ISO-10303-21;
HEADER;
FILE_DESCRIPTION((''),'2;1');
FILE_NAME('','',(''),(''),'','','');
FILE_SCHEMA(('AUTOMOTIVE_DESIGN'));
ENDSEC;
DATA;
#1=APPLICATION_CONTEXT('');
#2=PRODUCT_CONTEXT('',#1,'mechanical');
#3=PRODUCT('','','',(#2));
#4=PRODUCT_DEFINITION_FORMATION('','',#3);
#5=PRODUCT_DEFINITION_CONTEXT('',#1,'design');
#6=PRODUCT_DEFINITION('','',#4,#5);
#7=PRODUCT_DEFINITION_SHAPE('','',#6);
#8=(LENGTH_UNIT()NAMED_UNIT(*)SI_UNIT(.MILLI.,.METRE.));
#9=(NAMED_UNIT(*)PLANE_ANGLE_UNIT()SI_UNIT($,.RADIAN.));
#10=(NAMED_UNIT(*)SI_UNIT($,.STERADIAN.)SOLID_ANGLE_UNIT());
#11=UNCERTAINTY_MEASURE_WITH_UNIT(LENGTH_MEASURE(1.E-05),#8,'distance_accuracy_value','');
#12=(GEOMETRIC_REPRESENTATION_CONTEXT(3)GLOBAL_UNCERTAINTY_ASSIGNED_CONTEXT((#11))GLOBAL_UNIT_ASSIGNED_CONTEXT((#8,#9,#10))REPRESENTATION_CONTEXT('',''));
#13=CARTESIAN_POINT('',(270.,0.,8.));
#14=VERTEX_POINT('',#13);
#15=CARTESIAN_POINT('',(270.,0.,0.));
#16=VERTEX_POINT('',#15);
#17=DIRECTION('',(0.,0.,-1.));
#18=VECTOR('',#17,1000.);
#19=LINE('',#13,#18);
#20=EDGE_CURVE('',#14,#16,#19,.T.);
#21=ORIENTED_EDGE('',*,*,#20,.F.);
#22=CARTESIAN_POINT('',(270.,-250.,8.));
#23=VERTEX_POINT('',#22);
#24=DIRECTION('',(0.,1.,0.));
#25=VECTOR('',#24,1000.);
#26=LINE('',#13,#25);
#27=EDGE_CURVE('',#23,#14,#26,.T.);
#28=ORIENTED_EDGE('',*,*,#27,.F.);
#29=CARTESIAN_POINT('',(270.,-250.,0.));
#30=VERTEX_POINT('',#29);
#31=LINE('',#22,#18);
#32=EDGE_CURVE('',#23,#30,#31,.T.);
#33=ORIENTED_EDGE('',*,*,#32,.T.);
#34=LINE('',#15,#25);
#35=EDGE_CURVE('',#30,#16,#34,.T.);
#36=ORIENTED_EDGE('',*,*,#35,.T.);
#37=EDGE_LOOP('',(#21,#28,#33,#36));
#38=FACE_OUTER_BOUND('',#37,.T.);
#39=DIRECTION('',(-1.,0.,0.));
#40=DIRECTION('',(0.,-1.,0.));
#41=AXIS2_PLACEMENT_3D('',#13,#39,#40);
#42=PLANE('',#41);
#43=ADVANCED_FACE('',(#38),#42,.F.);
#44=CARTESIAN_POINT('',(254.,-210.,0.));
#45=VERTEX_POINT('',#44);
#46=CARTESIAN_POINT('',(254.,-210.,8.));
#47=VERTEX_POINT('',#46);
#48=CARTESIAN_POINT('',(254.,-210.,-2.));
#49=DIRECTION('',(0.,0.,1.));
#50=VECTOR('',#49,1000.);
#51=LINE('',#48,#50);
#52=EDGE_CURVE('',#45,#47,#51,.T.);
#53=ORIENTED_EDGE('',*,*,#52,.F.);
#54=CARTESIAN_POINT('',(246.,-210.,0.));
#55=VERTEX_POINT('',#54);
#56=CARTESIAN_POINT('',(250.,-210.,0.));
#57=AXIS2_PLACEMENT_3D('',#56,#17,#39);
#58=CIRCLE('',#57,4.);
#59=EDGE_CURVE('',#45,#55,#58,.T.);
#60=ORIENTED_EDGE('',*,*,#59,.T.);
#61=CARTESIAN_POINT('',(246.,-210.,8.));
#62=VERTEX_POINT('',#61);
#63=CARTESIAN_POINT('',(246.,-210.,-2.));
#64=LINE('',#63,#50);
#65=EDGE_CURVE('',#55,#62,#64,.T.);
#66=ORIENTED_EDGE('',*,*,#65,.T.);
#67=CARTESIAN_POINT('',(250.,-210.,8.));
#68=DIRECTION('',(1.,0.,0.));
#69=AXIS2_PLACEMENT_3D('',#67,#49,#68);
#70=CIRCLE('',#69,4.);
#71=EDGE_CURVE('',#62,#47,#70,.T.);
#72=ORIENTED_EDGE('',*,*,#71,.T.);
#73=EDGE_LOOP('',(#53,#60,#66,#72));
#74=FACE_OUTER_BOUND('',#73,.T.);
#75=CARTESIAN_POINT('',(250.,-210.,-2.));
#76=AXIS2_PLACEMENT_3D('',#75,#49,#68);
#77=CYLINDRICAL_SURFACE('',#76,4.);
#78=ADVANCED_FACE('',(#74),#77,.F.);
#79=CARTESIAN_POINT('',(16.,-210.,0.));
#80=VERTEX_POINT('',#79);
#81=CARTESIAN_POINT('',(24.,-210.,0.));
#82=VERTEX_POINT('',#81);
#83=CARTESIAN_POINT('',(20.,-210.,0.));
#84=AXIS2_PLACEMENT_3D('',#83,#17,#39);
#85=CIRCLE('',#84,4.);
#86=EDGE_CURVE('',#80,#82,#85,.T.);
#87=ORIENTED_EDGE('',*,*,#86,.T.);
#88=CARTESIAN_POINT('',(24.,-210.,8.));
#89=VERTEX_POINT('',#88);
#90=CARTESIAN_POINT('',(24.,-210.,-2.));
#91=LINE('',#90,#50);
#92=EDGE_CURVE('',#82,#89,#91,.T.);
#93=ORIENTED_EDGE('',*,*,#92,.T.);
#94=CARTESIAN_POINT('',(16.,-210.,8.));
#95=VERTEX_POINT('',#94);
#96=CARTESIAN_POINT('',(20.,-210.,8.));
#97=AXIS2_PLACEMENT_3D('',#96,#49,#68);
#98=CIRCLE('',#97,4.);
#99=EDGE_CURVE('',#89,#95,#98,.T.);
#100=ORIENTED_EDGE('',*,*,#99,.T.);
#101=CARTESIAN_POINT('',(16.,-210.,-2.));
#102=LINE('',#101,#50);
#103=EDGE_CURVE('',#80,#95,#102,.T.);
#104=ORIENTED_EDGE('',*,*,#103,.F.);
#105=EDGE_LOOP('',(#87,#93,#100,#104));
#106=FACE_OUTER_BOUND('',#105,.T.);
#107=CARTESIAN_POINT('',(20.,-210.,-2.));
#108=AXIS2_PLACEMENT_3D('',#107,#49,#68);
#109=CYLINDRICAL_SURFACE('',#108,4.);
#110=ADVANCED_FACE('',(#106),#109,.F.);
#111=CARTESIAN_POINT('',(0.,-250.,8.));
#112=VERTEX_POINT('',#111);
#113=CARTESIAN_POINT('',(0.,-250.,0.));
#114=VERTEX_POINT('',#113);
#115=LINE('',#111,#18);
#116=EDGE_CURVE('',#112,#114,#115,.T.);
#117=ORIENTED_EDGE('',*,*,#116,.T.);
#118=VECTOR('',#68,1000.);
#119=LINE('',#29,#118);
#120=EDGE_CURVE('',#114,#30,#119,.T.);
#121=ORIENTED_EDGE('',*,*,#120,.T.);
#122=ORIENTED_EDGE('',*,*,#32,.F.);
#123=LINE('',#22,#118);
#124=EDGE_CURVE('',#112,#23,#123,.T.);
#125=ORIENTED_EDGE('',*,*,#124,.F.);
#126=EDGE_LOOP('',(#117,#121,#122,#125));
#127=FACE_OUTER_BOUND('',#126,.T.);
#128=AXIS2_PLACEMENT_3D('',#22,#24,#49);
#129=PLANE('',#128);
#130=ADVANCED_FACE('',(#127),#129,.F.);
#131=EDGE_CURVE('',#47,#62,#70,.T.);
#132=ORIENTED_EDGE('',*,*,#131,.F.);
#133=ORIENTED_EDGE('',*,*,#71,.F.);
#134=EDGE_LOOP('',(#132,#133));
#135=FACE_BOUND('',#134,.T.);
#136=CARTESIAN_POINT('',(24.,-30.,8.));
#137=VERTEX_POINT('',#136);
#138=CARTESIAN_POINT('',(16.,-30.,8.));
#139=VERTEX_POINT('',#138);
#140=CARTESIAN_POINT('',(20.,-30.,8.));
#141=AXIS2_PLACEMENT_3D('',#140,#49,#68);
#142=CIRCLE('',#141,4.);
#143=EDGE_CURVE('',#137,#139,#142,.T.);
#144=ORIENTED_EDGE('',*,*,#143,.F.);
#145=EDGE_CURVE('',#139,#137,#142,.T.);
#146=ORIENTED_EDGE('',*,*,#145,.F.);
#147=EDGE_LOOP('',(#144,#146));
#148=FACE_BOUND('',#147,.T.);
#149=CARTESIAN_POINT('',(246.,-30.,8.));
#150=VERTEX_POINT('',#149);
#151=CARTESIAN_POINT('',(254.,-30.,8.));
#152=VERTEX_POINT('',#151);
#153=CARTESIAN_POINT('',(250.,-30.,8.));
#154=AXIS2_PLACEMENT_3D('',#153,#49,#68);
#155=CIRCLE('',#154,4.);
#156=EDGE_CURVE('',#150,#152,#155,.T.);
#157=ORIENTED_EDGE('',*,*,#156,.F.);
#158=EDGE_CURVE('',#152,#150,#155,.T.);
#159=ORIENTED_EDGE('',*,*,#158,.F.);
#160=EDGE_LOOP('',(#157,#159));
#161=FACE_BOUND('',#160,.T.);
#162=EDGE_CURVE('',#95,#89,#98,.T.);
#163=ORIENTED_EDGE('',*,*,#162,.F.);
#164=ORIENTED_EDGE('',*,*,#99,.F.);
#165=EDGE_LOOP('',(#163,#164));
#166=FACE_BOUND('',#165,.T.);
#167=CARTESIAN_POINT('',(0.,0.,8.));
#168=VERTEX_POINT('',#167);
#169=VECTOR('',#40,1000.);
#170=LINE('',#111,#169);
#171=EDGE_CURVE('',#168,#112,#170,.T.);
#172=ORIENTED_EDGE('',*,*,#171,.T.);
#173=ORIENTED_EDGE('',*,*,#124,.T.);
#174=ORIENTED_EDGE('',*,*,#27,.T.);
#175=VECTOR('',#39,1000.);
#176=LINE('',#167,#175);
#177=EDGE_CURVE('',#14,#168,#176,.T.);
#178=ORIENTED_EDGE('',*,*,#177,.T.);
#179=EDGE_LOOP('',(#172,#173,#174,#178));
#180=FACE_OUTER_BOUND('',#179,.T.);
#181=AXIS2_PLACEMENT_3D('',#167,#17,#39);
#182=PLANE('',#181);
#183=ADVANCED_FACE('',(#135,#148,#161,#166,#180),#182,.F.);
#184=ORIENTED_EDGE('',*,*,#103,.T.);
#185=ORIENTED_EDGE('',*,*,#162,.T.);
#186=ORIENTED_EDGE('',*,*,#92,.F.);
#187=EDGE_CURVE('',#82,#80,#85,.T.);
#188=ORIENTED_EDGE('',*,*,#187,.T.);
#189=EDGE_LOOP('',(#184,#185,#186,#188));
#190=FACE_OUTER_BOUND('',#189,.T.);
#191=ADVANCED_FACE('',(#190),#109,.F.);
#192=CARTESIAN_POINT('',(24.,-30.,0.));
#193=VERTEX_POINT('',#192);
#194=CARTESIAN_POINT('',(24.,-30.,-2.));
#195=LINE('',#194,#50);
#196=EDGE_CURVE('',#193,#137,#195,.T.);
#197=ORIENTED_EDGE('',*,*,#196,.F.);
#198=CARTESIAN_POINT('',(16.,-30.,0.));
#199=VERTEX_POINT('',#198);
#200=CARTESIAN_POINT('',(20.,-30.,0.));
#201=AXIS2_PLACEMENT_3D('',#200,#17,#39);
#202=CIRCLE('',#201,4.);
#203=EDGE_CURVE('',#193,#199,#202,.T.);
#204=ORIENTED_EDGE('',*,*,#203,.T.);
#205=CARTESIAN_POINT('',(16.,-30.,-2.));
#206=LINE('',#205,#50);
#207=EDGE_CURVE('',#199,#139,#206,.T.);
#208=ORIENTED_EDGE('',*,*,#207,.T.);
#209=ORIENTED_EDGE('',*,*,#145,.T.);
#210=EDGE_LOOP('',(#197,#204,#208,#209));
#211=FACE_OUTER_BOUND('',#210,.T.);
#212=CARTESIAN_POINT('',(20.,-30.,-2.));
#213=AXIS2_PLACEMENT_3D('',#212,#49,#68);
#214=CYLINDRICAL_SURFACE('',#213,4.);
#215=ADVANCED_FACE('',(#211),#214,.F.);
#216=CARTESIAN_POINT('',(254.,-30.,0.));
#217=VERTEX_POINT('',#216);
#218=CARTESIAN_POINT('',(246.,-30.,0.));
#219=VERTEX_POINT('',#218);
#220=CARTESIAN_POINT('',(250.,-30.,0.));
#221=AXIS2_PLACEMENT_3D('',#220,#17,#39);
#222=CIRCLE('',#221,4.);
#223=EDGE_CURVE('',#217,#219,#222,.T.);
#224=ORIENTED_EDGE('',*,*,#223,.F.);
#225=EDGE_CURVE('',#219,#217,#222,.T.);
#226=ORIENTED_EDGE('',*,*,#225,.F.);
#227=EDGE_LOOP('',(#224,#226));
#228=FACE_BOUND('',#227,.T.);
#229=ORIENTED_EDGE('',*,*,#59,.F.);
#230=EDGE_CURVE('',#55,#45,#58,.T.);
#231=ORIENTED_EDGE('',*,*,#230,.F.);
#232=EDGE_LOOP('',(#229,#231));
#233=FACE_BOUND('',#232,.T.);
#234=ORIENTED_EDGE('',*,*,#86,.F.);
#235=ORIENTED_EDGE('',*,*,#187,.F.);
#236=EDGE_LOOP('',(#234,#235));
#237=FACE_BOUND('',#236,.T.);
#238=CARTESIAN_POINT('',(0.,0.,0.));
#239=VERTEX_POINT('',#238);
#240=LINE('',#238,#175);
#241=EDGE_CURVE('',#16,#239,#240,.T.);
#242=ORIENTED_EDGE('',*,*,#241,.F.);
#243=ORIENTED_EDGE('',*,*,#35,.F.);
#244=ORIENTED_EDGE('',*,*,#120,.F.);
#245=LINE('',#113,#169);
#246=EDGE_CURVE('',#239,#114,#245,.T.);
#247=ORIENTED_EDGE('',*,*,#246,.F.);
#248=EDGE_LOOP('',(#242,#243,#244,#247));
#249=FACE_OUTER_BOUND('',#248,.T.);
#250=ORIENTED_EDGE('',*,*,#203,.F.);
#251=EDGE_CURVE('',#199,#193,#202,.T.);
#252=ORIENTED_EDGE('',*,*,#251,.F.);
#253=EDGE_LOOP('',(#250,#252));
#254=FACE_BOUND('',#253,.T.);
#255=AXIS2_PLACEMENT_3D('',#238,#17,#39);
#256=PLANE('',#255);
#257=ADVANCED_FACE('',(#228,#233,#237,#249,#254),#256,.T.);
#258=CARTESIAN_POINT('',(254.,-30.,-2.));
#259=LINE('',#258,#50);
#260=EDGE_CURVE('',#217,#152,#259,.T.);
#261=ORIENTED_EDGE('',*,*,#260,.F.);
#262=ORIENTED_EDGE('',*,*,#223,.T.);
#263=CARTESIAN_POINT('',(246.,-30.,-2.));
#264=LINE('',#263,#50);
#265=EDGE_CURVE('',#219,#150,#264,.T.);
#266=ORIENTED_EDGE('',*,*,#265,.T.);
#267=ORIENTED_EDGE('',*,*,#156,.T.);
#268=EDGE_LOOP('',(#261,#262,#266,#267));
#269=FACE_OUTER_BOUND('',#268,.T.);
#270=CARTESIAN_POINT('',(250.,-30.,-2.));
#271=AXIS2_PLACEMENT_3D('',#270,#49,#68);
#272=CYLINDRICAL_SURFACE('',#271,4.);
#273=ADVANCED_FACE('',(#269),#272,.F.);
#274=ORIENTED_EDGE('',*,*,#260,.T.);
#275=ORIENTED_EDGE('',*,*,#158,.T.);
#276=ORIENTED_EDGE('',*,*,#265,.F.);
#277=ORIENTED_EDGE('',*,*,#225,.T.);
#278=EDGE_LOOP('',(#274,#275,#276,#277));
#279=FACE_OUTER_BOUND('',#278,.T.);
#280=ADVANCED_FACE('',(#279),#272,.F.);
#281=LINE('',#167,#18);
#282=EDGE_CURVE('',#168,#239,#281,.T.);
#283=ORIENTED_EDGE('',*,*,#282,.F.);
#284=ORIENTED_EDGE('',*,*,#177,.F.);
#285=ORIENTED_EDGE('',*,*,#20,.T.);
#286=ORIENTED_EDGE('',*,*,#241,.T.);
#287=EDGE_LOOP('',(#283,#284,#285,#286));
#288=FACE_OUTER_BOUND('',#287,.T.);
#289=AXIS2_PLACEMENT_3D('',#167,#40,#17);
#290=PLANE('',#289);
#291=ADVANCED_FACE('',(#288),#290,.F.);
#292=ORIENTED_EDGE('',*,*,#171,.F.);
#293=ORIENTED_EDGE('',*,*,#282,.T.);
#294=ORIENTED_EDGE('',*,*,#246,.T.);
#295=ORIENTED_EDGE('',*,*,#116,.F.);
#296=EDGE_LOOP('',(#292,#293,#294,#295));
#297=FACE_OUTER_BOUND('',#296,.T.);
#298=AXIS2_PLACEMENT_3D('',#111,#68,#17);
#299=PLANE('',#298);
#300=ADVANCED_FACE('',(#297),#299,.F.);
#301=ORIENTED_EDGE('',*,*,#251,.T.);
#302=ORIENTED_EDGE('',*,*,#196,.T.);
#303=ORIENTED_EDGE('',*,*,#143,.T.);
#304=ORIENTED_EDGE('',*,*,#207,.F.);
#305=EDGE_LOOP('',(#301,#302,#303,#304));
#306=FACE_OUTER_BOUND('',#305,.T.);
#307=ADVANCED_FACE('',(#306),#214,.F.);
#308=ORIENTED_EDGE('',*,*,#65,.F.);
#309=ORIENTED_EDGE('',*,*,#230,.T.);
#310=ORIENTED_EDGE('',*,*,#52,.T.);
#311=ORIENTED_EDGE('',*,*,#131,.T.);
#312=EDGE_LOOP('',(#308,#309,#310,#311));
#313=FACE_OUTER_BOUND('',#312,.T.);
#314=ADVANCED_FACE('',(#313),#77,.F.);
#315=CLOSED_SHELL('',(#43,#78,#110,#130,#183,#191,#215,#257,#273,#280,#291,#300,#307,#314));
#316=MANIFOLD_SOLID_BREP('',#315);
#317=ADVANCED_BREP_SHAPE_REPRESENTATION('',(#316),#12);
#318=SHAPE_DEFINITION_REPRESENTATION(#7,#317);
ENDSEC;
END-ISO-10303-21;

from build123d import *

# Parameters (mm, degrees)
SKETCH_1_W          = 270
SKETCH_1_H          = 250
EXTRUDE_1_DEPTH     = 8
SKETCH_2_R          = 4
CUT_EXTRUDE_1_DEPTH = 10


with BuildPart() as part:
    # 草图1 → 凸台-拉伸1 (new body)
    with BuildSketch(Plane.XY):
        with Locations((135, -125)):
            Rectangle(SKETCH_1_W, SKETCH_1_H)
    extrude(amount=EXTRUDE_1_DEPTH)

    # 草图2 → 切除-拉伸1 (cut)
    with BuildSketch(Plane.XY.offset(8)):
        with Locations((250, -30)):
            Circle(SKETCH_2_R)
        with Locations((250, -210)):
            Circle(SKETCH_2_R)
        with Locations((20, -210)):
            Circle(SKETCH_2_R)
        with Locations((20, -30)):
            Circle(SKETCH_2_R)
    extrude(amount=-CUT_EXTRUDE_1_DEPTH, mode=Mode.SUBTRACT)


solid = part.part
